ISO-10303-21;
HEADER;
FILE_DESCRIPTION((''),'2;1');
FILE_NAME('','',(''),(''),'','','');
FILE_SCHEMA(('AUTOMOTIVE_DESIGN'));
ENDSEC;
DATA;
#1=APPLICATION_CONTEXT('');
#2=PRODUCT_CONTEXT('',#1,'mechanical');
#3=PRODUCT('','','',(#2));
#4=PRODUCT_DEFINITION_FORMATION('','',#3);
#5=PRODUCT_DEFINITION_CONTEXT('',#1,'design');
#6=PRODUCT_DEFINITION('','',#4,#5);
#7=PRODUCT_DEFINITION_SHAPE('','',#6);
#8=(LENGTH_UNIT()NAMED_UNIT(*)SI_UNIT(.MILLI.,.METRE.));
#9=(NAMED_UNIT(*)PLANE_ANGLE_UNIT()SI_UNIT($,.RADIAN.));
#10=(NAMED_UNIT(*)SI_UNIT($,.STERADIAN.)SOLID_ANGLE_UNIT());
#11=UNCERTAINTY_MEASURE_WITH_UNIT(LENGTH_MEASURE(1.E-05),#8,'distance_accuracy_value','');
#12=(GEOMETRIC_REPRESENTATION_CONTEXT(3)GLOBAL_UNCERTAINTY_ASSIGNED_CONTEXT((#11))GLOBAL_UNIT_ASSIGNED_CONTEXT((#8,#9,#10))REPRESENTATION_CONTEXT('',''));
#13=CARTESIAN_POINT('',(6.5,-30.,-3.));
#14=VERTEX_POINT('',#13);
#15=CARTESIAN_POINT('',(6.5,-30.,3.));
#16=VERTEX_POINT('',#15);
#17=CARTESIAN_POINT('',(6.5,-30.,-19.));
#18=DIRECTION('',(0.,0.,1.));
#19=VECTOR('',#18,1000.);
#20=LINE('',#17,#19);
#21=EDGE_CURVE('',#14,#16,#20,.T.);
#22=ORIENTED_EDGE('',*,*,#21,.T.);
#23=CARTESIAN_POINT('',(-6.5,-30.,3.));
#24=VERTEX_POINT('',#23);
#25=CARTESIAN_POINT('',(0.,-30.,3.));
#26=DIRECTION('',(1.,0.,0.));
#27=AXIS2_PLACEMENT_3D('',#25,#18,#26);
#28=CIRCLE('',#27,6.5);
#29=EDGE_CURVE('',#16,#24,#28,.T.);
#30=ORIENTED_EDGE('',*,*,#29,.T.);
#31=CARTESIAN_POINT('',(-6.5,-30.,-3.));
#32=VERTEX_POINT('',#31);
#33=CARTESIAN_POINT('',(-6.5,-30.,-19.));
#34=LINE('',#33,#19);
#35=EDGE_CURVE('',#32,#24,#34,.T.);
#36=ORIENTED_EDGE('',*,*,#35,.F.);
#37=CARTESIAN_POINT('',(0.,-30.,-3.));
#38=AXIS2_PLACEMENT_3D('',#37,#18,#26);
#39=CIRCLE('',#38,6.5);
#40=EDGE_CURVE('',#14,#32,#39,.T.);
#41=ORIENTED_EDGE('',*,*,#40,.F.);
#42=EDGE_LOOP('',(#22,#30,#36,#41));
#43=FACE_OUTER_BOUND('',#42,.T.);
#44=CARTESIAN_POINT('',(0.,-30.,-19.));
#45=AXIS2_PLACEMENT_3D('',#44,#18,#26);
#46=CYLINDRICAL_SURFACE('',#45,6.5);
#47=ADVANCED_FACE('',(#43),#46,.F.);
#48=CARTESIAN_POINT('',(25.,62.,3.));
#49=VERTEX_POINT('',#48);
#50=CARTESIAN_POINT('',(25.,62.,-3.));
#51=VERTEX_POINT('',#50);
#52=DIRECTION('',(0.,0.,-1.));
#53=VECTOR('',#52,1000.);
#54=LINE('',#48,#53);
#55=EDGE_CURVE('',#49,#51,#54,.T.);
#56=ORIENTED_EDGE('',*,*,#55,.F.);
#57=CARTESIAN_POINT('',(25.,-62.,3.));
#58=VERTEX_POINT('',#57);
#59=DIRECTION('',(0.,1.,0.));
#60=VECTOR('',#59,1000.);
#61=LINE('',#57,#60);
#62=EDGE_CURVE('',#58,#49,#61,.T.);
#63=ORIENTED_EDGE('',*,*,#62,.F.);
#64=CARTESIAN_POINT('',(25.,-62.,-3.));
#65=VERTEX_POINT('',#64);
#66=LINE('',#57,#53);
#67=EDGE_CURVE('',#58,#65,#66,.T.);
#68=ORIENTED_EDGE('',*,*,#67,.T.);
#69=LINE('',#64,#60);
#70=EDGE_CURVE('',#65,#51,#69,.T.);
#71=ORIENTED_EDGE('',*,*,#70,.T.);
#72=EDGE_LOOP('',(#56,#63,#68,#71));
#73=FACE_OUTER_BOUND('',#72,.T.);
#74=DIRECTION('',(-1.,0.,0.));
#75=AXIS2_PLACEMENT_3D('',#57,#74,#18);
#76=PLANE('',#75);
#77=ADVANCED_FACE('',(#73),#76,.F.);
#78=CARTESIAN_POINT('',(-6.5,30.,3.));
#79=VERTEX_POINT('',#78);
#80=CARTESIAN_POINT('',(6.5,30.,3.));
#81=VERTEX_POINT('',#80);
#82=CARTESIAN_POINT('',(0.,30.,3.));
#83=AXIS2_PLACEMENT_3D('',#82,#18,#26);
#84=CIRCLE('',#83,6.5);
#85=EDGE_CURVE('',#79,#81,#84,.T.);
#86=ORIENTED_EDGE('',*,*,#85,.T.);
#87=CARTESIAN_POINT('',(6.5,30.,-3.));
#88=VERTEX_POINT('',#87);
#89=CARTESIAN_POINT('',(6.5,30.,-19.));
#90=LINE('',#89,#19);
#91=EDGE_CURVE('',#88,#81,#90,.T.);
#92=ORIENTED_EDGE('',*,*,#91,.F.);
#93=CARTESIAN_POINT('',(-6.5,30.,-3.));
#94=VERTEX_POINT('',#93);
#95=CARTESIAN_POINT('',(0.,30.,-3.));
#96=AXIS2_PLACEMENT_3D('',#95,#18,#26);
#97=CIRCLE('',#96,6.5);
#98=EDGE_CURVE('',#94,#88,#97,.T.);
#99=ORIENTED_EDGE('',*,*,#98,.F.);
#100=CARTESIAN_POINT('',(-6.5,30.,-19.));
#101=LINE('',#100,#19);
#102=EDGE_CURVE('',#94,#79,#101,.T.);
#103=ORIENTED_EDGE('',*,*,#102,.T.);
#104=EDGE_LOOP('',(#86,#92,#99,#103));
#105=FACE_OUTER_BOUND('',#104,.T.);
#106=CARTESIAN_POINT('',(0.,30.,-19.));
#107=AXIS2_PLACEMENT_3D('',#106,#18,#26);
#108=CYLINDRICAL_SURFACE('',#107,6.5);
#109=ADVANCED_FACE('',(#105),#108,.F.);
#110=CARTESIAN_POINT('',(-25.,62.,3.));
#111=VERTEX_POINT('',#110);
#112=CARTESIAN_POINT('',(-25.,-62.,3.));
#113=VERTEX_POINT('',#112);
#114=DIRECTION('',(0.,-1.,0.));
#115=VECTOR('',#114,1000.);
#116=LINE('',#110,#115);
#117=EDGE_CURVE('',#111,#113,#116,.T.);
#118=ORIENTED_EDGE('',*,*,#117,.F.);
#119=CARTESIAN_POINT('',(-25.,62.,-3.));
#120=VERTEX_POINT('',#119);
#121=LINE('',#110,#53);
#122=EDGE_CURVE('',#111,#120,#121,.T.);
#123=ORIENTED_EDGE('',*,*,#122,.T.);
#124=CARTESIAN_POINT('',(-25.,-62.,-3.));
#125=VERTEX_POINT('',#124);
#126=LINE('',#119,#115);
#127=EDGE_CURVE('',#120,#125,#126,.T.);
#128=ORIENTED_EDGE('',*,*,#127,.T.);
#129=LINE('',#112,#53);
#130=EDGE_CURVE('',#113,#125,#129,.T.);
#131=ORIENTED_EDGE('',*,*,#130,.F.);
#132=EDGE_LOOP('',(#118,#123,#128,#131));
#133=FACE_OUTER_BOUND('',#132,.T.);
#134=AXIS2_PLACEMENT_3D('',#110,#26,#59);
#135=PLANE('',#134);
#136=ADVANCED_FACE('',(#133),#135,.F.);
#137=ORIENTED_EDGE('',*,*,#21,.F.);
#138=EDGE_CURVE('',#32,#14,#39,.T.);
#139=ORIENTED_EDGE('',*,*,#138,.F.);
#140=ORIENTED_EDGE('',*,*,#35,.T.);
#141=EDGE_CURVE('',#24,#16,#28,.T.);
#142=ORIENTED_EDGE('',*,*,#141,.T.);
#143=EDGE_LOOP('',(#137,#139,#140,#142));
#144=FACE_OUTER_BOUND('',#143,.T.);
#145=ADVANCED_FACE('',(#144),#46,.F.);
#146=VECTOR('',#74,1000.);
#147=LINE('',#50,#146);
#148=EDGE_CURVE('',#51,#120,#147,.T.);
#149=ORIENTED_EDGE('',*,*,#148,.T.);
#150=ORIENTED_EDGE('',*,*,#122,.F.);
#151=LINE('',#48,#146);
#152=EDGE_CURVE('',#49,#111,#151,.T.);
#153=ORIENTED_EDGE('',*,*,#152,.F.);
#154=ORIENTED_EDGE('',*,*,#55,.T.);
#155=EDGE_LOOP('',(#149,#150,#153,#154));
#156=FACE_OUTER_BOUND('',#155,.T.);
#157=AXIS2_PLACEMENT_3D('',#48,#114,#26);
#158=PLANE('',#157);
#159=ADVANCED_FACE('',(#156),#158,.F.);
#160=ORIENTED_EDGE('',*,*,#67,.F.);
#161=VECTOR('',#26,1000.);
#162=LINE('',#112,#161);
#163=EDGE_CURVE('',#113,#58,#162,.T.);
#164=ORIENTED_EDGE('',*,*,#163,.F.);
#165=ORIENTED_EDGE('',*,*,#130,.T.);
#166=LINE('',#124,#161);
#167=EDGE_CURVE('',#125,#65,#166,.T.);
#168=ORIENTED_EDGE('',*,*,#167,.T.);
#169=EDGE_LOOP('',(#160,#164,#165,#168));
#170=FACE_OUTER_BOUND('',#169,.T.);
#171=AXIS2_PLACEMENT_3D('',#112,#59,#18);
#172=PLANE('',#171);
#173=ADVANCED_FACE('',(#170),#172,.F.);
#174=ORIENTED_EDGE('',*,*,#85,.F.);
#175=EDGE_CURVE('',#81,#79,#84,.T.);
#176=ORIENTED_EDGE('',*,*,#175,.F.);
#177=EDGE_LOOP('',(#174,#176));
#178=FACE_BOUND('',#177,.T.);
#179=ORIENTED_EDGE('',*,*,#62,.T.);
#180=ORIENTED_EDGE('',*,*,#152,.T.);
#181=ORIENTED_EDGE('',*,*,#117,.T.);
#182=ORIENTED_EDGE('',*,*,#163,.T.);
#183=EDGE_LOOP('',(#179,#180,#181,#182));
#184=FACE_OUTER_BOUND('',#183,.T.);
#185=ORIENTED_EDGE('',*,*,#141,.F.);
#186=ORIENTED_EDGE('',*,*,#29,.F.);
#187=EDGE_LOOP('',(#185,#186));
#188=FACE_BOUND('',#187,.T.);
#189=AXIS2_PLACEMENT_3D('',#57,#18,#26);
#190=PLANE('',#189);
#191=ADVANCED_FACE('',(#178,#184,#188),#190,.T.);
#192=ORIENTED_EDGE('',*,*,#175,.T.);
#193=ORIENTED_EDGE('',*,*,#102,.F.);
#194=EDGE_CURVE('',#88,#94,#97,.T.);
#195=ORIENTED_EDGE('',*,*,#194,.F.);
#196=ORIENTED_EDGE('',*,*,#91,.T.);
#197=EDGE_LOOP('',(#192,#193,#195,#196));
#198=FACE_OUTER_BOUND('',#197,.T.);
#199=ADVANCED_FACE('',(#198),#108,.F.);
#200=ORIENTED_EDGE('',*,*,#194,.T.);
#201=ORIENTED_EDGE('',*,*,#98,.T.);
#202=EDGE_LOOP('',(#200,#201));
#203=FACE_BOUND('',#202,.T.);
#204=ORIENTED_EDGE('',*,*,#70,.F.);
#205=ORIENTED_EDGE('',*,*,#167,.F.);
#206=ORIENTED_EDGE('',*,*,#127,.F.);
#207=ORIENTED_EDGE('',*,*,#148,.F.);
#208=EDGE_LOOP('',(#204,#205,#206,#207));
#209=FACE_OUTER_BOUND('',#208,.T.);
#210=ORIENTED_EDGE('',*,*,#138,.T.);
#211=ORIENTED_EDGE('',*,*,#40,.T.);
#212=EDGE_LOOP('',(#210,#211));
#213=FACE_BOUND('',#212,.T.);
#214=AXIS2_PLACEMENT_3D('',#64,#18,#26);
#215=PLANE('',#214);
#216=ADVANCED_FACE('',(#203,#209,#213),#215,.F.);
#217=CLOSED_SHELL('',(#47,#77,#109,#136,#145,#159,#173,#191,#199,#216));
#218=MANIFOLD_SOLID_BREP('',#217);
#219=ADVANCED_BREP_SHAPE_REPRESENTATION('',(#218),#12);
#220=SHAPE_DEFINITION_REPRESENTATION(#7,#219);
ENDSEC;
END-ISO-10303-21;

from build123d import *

# Parameters (mm, degrees)
SKETCH1_W          = 50
SKETCH1_H          = 124
EXTRUDE1_DEPTH     = 3
SKETCH2_R          = 6.5
CUT_EXTRUDE1_DEPTH = 22


with BuildPart() as part:
    # Sketch1 → Extrude1 (new, symmetric)
    with BuildSketch(Plane.XY):
        Rectangle(SKETCH1_W, SKETCH1_H)
    extrude(amount=EXTRUDE1_DEPTH, both=True)

    # Sketch2 → Cut-Extrude1 (cut)
    with BuildSketch(Plane.XY.offset(3)):
        with Locations((0, 30)):
            Circle(SKETCH2_R)
        with Locations((0, -30)):
            Circle(SKETCH2_R)
    extrude(amount=-CUT_EXTRUDE1_DEPTH, mode=Mode.SUBTRACT)


solid = part.part
